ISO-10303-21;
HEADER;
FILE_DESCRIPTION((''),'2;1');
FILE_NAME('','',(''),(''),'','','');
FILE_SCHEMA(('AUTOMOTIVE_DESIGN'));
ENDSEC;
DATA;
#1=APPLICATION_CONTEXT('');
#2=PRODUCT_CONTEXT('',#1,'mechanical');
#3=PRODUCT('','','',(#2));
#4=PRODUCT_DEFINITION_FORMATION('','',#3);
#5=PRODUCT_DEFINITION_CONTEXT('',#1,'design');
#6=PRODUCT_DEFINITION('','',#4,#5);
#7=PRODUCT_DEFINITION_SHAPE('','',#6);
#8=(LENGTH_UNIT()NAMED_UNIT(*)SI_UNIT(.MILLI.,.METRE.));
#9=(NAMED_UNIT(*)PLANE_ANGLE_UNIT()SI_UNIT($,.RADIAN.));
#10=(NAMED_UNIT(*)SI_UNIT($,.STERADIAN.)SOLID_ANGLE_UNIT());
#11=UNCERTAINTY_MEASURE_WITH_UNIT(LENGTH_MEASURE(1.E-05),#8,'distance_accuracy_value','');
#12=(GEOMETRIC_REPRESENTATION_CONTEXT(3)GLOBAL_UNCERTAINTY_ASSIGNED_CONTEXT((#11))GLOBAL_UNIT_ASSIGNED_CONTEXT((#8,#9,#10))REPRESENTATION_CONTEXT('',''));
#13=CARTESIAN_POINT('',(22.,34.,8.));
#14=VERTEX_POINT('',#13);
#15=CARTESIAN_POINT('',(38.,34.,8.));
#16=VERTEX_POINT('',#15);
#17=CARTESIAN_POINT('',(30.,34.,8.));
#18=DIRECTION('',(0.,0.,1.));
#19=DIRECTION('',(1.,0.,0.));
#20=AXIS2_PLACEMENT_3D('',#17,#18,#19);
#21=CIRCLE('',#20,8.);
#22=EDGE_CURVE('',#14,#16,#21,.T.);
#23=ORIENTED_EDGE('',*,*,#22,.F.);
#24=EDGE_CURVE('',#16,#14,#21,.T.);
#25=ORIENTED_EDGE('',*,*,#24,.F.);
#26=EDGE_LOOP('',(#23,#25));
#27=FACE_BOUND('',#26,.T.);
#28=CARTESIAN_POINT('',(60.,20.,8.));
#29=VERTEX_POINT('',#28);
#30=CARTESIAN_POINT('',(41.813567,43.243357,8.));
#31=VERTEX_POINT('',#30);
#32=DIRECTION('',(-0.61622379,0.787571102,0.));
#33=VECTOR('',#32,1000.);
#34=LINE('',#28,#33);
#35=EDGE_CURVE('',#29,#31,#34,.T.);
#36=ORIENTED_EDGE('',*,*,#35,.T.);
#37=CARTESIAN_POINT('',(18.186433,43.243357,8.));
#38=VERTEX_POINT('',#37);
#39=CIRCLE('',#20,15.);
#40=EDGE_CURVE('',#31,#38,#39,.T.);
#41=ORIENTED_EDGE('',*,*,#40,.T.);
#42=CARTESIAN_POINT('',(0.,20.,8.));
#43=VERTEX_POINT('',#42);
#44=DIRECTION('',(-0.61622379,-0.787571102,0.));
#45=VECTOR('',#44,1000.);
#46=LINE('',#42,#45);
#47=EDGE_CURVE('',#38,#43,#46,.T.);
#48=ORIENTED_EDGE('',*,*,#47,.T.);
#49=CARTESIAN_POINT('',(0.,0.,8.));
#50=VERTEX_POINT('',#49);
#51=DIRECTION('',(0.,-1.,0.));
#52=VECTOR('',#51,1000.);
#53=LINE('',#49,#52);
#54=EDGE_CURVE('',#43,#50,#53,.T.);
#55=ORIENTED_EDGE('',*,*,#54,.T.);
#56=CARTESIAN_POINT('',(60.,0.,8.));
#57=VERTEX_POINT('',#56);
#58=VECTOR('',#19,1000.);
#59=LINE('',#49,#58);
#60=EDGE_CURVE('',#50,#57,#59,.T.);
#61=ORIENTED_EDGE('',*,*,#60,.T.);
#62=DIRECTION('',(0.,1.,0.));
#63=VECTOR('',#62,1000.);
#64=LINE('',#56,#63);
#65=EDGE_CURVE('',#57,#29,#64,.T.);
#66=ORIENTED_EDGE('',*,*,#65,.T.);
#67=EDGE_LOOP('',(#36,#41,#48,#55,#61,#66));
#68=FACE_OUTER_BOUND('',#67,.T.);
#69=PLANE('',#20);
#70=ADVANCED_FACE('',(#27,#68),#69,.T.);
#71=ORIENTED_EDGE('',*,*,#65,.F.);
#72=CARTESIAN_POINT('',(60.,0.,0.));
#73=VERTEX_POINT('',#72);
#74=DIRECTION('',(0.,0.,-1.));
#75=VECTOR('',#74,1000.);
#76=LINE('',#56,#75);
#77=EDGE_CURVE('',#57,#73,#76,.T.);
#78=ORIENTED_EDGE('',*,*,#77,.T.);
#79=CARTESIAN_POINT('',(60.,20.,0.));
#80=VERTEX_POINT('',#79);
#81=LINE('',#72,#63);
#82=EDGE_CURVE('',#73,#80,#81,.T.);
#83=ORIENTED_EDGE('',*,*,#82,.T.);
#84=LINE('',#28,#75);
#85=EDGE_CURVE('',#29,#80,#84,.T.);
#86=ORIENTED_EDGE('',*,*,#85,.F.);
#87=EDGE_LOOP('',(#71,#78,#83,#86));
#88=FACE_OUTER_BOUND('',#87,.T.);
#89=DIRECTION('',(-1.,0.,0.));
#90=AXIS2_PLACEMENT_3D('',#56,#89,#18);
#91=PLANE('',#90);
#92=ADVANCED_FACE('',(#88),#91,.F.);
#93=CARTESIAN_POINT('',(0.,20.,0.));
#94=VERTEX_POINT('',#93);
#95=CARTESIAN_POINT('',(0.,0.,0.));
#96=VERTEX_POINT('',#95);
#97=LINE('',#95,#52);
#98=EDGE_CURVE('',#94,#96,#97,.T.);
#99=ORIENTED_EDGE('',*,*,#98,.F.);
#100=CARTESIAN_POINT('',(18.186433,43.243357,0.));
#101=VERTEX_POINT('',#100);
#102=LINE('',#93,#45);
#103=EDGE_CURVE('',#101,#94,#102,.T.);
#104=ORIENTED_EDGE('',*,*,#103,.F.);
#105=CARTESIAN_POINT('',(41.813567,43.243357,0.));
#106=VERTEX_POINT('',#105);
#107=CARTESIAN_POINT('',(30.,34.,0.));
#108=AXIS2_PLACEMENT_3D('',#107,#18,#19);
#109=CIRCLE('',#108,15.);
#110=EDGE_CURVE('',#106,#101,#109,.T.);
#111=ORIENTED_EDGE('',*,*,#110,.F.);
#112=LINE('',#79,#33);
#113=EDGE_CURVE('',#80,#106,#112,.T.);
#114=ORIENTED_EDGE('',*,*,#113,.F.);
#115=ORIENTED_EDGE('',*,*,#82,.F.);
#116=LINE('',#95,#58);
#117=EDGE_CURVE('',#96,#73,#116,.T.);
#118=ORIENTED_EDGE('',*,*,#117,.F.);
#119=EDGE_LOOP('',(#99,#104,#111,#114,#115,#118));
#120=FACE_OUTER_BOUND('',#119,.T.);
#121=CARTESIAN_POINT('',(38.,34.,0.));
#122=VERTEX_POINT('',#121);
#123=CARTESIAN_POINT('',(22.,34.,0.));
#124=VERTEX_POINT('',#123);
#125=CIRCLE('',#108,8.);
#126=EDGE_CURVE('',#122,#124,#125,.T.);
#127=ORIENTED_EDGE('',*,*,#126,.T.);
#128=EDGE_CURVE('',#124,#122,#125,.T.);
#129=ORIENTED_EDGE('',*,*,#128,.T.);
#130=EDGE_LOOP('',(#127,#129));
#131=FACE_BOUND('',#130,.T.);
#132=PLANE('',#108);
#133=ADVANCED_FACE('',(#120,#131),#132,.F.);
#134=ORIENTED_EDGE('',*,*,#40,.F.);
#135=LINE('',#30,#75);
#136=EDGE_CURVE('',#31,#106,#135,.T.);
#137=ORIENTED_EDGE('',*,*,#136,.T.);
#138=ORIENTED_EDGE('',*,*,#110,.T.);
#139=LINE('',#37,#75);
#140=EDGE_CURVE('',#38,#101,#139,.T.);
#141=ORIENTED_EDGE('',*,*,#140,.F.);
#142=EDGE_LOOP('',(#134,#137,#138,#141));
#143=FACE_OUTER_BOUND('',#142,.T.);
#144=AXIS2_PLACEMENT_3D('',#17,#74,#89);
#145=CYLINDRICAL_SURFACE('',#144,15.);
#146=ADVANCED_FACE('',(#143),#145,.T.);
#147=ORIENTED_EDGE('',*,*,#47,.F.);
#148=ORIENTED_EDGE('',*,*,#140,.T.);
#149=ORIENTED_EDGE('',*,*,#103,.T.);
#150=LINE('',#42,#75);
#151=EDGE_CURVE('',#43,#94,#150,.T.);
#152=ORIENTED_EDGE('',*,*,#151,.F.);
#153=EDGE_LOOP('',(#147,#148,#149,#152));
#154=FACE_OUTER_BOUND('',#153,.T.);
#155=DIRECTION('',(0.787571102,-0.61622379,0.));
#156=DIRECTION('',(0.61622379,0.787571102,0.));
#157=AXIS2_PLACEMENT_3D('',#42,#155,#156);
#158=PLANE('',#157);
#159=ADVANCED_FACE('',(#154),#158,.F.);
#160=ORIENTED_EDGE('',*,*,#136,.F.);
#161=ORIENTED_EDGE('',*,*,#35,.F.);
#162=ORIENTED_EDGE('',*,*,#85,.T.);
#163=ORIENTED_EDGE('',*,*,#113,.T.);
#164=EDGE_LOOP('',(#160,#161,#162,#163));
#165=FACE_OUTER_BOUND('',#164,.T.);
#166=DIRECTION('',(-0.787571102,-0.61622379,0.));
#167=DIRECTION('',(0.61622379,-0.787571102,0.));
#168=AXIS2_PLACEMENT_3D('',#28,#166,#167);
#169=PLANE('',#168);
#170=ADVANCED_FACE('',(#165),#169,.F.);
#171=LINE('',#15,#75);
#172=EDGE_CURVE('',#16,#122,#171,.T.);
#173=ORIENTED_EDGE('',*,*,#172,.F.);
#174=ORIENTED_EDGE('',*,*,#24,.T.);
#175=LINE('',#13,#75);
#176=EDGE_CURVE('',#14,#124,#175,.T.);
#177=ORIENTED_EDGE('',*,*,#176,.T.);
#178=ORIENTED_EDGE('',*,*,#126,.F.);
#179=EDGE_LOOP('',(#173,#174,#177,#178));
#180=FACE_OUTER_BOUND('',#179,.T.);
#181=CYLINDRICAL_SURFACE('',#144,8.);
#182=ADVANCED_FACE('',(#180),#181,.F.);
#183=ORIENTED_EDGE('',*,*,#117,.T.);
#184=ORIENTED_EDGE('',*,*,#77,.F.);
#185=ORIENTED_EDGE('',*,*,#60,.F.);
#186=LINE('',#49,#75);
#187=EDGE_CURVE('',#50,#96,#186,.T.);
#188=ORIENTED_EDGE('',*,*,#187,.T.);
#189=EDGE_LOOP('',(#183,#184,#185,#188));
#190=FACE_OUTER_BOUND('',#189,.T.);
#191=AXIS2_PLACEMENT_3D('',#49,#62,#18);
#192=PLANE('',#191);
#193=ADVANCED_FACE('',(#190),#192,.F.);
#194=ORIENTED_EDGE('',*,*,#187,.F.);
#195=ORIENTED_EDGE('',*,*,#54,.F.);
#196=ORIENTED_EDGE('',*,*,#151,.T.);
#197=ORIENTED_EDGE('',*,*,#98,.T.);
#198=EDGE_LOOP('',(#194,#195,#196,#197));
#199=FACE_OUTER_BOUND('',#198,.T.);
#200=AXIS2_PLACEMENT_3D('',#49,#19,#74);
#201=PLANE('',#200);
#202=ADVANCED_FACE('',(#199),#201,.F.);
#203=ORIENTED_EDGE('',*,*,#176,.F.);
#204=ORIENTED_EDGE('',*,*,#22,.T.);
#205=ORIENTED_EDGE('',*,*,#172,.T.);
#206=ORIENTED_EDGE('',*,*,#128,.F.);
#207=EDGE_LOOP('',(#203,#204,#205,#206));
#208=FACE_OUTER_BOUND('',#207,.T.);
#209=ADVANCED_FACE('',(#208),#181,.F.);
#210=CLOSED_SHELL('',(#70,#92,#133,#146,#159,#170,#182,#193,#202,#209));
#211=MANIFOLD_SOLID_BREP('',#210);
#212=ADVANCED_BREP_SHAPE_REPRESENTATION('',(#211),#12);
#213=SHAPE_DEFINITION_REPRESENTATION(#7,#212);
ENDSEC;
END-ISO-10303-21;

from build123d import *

# Parameters (mm, degrees)
SKETCH1_R           = 8
BOSS_EXTRUDE1_DEPTH = 8


with BuildPart() as part:
    # Sketch1 → Boss-Extrude1 (new body)
    with BuildSketch(Plane.XY):
        with BuildLine():
            Line((0, 0), (0, 20))
            Line((0, 20), (18.18643347, 43.243356849))
            ThreePointArc((18.18643347, 43.243356849), (30, 49), (41.81356653, 43.243356849))
            Line((41.81356653, 43.243356849), (60, 20))
            Line((60, 20), (60, 0))
            Line((60, 0), (0, 0))
        make_face()
        with Locations((30, 34)):
            Circle(SKETCH1_R, mode=Mode.SUBTRACT)
    extrude(amount=BOSS_EXTRUDE1_DEPTH)


solid = part.part
